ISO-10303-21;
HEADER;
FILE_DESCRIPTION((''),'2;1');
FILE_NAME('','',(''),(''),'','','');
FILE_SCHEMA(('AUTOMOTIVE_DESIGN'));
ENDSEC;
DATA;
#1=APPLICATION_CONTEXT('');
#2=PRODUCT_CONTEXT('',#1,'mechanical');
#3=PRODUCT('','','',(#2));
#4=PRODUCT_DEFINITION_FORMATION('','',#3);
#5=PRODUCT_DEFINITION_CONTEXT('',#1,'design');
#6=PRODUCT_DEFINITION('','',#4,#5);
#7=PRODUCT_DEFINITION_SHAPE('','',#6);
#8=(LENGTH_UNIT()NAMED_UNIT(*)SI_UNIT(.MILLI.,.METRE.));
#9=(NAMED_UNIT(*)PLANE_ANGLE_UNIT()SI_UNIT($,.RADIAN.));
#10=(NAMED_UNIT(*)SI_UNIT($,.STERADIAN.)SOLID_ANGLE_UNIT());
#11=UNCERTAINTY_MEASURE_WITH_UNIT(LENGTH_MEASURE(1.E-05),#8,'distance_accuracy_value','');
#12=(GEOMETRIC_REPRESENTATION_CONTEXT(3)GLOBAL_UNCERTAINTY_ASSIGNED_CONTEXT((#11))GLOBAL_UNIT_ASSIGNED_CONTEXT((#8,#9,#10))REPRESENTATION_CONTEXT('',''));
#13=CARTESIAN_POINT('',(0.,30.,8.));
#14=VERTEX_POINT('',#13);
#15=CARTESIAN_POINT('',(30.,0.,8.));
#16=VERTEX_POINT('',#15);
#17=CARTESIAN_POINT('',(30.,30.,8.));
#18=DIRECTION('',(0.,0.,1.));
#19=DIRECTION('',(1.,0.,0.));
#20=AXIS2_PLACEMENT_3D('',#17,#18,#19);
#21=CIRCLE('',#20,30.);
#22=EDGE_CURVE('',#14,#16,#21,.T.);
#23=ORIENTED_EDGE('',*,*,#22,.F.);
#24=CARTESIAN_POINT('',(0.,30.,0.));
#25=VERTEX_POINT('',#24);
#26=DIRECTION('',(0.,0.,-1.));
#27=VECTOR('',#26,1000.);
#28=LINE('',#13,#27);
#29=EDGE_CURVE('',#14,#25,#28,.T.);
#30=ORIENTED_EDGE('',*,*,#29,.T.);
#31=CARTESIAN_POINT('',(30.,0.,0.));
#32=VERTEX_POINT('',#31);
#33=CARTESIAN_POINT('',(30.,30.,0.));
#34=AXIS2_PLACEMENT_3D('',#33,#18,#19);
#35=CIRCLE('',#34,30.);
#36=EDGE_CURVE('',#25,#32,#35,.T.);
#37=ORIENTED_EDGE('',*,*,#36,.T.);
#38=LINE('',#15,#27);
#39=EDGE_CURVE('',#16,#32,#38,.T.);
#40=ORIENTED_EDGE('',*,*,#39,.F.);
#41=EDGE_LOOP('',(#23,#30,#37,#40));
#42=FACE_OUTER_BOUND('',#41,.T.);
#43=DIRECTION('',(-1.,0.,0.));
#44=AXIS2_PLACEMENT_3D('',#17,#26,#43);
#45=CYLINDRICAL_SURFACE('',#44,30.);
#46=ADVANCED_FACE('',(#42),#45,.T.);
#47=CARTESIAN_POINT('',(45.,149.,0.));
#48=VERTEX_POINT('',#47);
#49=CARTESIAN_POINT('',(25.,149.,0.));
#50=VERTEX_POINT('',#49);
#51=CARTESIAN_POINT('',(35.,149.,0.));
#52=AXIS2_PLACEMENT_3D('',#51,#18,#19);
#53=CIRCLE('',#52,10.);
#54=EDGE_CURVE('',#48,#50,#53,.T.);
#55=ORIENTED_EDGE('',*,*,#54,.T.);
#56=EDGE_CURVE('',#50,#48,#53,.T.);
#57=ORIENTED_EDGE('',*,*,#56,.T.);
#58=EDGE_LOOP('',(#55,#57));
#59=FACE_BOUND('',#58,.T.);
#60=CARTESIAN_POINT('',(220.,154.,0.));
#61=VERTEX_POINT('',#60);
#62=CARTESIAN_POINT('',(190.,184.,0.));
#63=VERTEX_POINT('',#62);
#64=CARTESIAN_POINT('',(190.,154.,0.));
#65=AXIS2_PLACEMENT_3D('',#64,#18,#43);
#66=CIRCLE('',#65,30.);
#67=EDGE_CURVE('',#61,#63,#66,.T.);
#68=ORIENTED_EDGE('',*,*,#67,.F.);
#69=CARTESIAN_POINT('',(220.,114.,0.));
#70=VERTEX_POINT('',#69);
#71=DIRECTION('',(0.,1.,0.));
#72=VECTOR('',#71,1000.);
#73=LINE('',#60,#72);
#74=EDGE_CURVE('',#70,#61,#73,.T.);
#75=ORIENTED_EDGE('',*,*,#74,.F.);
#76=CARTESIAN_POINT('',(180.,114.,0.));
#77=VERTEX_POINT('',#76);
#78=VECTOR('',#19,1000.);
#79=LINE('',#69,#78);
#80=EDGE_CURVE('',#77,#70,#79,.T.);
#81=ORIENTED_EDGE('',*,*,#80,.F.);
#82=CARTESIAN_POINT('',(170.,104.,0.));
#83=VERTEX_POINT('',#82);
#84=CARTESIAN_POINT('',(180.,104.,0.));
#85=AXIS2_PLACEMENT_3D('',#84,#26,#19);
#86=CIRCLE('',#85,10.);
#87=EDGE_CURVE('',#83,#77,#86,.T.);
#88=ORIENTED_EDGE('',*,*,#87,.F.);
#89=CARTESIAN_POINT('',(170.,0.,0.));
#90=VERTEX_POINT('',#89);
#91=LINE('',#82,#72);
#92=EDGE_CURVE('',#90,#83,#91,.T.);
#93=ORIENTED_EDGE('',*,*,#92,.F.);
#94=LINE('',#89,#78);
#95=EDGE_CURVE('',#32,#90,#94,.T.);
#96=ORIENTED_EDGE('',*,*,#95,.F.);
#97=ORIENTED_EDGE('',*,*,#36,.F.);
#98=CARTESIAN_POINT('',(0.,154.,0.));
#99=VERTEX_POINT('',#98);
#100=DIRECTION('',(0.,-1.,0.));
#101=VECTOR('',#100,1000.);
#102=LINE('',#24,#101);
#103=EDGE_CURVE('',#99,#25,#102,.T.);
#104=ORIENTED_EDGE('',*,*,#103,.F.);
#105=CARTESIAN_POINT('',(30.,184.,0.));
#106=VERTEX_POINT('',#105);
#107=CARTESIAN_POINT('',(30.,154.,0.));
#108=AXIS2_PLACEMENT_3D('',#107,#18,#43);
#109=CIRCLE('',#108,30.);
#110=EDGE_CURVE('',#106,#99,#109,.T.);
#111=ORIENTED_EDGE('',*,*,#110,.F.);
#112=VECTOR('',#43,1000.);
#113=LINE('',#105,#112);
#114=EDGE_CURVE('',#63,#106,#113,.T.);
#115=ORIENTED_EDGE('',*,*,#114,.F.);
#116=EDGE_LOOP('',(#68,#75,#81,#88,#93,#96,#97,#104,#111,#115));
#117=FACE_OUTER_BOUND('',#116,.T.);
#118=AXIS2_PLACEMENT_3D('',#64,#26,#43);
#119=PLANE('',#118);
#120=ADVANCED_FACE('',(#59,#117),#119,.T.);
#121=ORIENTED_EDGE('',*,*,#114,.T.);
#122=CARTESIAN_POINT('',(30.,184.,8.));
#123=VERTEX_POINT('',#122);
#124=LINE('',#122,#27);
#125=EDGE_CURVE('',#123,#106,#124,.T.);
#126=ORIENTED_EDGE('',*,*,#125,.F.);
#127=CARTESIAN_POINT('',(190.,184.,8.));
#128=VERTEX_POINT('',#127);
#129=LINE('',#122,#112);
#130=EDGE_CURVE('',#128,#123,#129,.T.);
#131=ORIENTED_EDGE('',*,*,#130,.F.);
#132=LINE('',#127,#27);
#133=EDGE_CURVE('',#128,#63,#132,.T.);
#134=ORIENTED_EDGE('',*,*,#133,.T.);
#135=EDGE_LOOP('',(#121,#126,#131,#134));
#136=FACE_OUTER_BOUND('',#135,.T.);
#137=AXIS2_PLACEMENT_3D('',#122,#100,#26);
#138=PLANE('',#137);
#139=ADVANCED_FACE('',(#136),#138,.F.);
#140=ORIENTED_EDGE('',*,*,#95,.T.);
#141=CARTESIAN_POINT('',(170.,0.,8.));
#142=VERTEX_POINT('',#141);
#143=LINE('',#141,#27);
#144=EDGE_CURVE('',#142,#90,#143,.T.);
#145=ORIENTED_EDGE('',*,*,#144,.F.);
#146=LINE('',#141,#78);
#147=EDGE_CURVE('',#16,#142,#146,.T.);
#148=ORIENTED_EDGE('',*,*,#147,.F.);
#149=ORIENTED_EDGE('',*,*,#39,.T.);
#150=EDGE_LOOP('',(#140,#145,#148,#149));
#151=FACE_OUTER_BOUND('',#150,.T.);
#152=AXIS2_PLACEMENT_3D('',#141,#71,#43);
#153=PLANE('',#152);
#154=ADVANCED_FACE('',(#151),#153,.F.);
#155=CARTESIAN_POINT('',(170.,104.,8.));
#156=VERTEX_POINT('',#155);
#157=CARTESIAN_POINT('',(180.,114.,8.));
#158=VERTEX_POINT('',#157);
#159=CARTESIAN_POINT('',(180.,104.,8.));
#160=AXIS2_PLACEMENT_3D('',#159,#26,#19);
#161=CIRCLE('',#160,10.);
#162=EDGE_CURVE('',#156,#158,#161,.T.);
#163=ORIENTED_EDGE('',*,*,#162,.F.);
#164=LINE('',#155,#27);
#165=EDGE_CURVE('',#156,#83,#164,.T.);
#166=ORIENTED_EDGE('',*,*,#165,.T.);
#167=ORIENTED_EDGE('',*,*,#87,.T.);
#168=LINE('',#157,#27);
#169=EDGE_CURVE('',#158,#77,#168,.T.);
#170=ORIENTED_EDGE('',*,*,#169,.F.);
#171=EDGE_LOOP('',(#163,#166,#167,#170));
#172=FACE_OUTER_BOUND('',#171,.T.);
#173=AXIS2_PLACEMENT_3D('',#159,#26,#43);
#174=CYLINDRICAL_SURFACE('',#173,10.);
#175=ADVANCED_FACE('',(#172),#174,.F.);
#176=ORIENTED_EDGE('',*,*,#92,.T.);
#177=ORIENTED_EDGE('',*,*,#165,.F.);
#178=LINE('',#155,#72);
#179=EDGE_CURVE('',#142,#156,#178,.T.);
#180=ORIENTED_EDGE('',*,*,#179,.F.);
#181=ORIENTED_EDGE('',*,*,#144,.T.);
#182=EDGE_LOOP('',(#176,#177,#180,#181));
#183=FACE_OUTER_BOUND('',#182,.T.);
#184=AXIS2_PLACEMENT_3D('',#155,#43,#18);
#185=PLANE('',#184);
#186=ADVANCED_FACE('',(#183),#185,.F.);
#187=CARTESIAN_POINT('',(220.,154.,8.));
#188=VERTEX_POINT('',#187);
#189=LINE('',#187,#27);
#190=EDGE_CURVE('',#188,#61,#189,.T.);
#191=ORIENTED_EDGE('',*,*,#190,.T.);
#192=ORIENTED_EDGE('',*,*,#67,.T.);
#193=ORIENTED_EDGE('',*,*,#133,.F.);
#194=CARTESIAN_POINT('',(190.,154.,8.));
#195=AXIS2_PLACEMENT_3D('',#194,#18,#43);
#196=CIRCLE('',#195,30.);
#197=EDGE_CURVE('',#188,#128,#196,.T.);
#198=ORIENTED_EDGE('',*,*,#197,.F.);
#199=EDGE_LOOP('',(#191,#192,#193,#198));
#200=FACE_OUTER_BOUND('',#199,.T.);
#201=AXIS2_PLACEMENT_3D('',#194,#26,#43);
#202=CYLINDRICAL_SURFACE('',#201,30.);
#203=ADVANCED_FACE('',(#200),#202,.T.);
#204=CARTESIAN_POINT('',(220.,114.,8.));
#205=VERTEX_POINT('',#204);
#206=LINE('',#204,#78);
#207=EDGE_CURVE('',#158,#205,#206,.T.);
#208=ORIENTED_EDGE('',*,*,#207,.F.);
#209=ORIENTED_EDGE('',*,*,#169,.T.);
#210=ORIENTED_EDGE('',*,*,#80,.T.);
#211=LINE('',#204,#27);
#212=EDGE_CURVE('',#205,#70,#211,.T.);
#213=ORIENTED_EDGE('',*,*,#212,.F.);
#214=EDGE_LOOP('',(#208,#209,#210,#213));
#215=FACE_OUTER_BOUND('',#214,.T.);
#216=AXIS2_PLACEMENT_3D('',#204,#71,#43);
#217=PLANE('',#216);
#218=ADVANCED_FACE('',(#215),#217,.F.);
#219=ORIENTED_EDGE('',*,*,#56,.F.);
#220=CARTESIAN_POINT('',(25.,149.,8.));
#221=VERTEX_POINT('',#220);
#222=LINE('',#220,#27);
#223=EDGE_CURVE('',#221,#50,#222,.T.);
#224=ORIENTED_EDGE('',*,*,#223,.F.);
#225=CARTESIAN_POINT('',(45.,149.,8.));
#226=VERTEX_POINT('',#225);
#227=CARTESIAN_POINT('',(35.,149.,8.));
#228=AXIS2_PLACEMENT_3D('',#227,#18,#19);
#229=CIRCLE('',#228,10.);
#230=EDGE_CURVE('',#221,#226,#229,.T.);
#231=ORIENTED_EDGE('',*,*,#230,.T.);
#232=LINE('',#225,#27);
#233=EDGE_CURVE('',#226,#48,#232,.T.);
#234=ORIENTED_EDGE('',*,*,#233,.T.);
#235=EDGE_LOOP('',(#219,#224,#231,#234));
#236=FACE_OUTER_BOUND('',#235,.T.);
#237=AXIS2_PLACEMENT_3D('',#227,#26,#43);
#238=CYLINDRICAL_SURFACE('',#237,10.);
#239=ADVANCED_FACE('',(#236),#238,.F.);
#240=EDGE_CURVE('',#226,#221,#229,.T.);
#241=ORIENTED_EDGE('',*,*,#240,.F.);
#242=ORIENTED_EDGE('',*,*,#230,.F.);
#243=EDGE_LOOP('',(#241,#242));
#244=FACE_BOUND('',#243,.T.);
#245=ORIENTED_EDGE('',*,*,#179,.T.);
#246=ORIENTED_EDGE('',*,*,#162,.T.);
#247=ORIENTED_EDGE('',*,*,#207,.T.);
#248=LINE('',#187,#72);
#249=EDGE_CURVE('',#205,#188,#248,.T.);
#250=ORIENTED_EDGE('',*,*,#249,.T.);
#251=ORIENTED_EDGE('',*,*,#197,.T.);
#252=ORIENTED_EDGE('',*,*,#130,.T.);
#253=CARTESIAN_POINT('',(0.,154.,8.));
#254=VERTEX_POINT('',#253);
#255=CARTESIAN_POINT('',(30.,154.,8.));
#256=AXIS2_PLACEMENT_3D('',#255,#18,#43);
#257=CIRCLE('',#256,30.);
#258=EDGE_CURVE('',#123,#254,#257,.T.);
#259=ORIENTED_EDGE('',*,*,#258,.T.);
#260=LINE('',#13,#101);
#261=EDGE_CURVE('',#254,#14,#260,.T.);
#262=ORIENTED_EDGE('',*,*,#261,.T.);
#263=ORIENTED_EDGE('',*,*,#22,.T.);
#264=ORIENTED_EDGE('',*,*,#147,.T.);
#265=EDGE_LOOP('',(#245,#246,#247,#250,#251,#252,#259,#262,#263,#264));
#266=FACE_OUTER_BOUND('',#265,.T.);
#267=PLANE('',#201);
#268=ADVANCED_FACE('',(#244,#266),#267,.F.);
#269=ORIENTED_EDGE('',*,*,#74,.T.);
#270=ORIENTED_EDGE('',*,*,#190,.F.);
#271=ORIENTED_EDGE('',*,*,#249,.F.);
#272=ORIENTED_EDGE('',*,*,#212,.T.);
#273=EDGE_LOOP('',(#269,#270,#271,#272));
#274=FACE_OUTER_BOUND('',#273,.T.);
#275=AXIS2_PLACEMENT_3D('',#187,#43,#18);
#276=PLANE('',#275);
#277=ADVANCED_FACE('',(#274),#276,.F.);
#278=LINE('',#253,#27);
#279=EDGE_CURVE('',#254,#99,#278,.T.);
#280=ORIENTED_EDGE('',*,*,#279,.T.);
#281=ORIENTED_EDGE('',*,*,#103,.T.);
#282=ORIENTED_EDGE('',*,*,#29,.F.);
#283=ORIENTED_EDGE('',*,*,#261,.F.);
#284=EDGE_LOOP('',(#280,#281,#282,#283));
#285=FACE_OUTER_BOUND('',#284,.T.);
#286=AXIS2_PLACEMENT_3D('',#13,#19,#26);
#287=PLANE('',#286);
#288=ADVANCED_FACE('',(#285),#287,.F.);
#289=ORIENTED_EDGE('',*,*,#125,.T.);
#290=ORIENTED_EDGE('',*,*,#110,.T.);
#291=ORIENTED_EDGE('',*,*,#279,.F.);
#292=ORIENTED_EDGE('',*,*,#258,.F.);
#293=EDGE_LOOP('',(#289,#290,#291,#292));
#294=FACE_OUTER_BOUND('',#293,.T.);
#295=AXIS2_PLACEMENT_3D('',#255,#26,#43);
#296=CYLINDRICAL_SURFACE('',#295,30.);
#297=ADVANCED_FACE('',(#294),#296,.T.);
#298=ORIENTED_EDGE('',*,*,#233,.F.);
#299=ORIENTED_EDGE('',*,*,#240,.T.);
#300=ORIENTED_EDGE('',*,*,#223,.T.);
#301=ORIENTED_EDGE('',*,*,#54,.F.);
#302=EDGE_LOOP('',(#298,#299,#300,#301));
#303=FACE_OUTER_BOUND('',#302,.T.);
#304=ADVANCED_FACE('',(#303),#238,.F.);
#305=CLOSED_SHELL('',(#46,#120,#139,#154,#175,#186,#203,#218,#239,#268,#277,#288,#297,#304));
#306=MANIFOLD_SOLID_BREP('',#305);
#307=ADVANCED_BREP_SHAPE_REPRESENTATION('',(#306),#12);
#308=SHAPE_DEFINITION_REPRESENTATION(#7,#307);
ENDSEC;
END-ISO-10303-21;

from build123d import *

# Parameters (mm, degrees)
SKETCH1_R           = 10
BOSS_EXTRUDE1_DEPTH = 8


with BuildPart() as part:
    # Sketch1 → Boss-Extrude1 (new body)
    with BuildSketch(Plane.XY):
        with BuildLine():
            Line((0, 30), (0, 154))
            ThreePointArc((0, 154), (8.786796564, 175.213203436), (30, 184))
            Line((30, 184), (190, 184))
            ThreePointArc((190, 184), (211.213203436, 175.213203436), (220, 154))
            Line((220, 154), (220, 114))
            Line((220, 114), (180, 114))
            ThreePointArc((180, 114), (172.928932188, 111.071067812), (170, 104))
            Line((170, 104), (170, 0))
            Line((170, 0), (30, 0))
            ThreePointArc((30, 0), (8.786796564, 8.786796564), (0, 30))
        make_face()
        with Locations((35, 149)):
            Circle(SKETCH1_R, mode=Mode.SUBTRACT)
    extrude(amount=BOSS_EXTRUDE1_DEPTH)


solid = part.part
